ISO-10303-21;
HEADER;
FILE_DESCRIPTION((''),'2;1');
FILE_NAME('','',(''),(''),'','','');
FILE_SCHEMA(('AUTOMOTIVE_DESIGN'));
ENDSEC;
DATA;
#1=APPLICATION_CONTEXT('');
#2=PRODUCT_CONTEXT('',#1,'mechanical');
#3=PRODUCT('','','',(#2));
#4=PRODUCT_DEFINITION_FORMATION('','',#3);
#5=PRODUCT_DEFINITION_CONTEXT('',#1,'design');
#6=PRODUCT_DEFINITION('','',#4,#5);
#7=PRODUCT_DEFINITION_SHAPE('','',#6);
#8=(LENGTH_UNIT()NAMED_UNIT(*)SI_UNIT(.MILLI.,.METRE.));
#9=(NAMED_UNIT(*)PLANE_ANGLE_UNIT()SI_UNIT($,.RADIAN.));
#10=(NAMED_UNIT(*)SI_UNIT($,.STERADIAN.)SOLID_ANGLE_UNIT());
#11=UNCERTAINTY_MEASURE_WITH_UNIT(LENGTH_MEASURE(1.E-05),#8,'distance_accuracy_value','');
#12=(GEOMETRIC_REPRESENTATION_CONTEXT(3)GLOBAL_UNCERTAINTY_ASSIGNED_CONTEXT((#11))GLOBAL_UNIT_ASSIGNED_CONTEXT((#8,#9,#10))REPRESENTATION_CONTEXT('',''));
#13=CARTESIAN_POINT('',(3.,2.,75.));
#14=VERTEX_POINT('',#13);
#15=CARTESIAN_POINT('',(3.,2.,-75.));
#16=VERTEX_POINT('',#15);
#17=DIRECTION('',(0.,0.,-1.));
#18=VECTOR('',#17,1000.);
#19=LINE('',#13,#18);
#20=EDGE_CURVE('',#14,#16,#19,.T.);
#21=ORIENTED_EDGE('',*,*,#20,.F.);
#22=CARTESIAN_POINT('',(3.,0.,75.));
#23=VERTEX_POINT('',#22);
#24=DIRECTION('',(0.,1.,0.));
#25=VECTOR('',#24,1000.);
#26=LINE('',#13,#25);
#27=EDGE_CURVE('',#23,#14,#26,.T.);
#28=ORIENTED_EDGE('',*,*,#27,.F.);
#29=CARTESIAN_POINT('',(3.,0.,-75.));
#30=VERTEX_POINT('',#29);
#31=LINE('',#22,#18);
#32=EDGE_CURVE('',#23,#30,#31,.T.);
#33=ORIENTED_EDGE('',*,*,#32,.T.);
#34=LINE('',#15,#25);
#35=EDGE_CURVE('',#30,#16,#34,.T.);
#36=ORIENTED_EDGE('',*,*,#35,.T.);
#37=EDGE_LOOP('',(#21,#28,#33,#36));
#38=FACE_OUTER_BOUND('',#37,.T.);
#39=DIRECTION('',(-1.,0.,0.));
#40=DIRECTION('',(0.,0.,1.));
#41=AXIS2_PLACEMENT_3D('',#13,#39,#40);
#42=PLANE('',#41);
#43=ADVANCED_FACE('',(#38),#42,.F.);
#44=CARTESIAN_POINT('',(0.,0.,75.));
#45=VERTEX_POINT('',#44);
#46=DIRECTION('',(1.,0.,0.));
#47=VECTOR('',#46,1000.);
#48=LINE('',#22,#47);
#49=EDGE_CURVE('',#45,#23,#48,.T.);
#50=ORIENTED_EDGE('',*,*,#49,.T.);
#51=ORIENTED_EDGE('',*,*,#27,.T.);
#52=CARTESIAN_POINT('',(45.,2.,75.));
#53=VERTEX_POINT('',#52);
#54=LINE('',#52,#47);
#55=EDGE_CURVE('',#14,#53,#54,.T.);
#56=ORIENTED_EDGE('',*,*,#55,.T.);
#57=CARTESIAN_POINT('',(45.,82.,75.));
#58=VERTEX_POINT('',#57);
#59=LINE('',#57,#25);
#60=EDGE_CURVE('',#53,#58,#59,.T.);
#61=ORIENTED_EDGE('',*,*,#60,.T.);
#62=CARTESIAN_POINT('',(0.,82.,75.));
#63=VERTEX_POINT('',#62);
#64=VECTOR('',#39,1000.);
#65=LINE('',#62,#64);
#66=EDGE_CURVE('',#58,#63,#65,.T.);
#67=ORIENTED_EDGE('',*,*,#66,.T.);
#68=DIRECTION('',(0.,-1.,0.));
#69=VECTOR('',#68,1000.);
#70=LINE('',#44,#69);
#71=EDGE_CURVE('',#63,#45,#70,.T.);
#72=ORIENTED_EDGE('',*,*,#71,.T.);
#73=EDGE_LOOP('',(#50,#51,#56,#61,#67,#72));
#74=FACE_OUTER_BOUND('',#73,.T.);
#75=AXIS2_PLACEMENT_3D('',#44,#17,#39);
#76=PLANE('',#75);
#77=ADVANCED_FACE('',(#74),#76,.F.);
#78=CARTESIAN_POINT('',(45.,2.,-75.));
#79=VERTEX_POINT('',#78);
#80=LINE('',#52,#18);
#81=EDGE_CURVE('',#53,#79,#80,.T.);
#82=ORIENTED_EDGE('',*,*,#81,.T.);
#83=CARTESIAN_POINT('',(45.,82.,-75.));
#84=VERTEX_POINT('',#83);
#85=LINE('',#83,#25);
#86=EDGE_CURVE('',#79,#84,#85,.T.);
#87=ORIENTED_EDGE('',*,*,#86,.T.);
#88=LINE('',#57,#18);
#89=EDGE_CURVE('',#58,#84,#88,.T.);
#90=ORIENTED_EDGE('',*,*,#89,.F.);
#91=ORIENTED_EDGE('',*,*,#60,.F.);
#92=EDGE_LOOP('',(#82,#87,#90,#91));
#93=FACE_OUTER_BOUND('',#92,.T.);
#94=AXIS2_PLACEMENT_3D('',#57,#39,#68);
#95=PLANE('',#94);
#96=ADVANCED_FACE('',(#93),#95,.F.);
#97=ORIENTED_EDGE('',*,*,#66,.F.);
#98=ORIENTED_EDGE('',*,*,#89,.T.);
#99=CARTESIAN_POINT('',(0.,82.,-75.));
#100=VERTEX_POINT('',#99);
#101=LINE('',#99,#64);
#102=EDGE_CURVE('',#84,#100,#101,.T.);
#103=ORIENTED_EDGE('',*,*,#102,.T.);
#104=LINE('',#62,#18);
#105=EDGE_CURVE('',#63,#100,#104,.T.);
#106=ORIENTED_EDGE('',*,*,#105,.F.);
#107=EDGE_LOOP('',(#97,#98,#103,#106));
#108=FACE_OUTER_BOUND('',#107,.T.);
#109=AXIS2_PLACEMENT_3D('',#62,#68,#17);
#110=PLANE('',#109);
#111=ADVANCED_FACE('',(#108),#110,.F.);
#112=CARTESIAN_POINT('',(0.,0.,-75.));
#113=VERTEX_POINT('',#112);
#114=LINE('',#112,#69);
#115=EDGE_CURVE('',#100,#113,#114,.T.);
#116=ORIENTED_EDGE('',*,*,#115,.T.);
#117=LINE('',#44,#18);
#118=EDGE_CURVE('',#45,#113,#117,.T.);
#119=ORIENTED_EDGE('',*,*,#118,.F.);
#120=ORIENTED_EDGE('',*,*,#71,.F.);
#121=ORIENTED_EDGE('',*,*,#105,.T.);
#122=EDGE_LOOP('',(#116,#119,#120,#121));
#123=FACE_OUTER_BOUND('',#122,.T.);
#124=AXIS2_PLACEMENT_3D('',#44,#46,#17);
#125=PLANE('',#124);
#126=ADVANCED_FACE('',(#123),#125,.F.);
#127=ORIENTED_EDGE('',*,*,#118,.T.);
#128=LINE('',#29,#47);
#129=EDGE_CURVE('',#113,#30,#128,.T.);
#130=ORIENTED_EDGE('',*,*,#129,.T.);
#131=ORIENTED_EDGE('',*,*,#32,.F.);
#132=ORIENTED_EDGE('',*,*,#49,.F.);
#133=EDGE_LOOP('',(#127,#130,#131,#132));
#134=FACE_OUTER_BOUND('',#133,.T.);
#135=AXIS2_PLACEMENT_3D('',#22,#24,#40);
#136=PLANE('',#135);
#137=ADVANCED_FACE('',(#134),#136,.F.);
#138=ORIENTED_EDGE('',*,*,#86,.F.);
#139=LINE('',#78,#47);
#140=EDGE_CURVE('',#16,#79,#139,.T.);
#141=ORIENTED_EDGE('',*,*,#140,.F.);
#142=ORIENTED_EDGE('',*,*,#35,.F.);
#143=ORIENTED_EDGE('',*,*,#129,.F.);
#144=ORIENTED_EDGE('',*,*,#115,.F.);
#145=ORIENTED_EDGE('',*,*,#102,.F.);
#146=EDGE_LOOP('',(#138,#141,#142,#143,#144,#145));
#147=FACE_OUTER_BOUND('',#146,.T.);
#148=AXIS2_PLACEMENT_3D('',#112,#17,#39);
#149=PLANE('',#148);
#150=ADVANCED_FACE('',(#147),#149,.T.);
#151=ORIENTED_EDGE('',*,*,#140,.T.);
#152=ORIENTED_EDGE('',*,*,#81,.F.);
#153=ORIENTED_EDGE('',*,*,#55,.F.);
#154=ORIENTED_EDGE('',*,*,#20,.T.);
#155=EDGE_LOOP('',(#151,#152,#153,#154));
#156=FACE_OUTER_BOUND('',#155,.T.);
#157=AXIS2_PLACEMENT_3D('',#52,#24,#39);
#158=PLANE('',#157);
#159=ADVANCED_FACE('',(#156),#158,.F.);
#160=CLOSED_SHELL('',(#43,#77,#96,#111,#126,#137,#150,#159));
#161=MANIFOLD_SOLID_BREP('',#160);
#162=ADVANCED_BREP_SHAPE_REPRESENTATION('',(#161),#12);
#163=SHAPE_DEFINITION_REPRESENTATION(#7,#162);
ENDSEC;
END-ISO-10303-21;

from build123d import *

# Parameters (mm, degrees)
EXTRUDE_1_DEPTH = 75


with BuildPart() as part:
    # 草图1 → 凸台-拉伸1 (new, symmetric)
    with BuildSketch(Plane.XY):
        Polygon((0, 0), (0, 82), (45, 82), (45, 2), (3, 2), (3, 0), align=None)
    extrude(amount=EXTRUDE_1_DEPTH, both=True)


solid = part.part
